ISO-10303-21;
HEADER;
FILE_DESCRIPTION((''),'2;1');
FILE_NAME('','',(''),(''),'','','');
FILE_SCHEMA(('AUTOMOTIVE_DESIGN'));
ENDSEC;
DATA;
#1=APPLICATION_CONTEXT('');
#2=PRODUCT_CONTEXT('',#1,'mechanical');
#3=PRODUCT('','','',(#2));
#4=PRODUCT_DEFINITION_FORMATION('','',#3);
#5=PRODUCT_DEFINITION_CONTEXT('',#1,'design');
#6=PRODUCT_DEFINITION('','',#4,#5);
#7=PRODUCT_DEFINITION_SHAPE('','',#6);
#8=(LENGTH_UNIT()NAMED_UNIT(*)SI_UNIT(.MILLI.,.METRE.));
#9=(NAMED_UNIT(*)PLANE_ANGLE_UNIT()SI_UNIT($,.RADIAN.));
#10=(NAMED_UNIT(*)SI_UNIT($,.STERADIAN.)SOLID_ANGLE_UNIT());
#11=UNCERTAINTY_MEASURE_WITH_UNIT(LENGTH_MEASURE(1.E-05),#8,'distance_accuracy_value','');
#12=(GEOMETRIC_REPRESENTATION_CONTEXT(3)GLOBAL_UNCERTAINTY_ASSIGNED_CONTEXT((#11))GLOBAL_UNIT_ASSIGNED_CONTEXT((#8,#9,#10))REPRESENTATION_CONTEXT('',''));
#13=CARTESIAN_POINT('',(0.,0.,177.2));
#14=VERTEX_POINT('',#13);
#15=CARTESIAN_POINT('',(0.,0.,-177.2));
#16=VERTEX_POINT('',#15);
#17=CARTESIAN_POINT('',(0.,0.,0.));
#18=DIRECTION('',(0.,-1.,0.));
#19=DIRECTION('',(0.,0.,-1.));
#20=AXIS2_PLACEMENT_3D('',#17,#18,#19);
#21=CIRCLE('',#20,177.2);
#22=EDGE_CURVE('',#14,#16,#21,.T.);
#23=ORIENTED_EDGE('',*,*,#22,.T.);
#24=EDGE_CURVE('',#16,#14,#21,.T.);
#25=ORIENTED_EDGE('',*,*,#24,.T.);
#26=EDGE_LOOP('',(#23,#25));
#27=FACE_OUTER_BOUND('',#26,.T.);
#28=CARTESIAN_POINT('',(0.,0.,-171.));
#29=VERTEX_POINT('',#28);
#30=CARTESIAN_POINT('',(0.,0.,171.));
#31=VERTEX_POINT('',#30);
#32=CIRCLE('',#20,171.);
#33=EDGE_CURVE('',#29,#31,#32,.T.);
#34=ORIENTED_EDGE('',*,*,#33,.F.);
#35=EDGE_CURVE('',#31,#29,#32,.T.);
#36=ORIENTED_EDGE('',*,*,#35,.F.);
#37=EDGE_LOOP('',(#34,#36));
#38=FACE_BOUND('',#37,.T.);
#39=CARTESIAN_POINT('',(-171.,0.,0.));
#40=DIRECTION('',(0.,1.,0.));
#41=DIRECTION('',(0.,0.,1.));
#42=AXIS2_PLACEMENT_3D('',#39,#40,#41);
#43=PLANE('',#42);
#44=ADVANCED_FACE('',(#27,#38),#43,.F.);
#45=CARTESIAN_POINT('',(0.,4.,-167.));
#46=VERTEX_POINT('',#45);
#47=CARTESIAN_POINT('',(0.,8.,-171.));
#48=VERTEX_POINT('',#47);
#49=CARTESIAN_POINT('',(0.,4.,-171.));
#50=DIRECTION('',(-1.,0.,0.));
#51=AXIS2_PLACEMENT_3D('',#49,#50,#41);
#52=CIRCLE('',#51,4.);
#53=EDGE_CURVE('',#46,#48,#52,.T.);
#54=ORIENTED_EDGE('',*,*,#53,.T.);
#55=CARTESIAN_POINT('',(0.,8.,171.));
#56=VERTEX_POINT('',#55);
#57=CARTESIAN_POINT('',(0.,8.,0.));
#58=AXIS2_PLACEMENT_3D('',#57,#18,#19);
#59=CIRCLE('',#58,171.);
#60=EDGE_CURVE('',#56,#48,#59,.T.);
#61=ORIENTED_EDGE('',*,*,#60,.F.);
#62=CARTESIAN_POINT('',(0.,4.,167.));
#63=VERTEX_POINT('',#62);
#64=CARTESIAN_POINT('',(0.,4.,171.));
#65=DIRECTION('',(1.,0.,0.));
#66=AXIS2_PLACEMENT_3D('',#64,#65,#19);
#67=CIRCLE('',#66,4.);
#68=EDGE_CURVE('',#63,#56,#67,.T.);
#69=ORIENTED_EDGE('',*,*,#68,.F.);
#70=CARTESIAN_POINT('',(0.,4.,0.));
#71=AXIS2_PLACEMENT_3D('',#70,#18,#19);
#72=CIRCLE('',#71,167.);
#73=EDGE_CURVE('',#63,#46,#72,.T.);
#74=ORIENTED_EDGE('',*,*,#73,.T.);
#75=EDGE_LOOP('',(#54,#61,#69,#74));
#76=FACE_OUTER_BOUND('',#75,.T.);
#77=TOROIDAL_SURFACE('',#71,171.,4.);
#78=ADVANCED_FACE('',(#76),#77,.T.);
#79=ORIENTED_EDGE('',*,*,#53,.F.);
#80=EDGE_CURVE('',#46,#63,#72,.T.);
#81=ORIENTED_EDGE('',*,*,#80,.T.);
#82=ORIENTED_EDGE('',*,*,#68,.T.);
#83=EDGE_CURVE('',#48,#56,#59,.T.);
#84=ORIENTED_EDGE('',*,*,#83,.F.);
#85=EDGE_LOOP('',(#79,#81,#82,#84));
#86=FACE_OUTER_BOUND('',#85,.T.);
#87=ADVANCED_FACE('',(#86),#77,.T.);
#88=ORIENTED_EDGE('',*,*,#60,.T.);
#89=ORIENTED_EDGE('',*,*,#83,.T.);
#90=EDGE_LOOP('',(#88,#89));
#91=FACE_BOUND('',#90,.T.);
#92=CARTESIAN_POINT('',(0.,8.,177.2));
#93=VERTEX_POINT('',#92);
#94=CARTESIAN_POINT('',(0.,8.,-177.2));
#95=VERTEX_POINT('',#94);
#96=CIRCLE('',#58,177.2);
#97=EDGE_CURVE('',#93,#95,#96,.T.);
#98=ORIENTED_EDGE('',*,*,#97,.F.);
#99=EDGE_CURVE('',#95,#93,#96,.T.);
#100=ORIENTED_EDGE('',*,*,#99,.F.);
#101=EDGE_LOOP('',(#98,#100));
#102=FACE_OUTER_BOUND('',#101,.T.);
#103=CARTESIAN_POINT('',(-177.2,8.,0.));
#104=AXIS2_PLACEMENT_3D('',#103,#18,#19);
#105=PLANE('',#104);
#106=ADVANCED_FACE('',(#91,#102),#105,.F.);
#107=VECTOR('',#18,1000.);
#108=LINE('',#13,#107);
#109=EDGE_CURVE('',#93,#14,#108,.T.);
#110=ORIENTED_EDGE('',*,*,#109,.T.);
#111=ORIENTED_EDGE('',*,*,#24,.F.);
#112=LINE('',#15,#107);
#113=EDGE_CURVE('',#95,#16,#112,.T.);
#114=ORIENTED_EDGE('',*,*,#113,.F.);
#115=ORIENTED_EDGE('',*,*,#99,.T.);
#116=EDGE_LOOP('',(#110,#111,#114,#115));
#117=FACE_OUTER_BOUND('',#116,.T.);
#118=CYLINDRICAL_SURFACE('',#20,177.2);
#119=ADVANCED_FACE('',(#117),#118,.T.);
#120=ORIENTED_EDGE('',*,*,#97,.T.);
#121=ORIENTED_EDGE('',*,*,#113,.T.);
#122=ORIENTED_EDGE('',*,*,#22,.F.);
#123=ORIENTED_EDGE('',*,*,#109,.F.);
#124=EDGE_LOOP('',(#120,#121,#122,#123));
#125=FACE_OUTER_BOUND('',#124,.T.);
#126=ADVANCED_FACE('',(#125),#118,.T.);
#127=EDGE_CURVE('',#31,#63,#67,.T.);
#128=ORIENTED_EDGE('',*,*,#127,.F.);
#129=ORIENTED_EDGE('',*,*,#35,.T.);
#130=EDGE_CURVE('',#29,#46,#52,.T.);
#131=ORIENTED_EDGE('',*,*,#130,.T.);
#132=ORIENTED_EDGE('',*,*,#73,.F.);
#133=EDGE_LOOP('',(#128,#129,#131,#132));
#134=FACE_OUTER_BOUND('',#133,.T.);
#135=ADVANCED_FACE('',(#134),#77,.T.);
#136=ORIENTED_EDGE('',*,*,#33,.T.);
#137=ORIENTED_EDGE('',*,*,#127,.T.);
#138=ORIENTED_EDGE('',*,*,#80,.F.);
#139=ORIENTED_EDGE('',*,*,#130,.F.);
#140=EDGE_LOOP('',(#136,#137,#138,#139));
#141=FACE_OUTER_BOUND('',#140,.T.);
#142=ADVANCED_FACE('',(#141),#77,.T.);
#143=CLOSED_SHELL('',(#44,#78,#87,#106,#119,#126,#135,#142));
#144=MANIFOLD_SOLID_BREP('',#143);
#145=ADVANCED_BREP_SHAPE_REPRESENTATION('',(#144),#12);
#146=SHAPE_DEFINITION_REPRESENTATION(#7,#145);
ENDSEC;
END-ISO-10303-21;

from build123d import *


with BuildPart() as part:
    # Sketch1 → Revolve1 (revolve)
    with BuildSketch(Plane.XY, mode=Mode.PRIVATE) as revolve1_sk:
        with BuildLine():
            Line((-171, 0), (-177.2, 0))
            Line((-177.2, 0), (-177.2, 8))
            Line((-177.2, 8), (-171, 8))
            ThreePointArc((-171, 8), (-167, 4), (-171, 0))
        make_face()
    revolve(revolve1_sk.sketch.rotate(Axis((0, 0, 0), (0, 1, 0)), 270), axis=Axis((0, 0, 0), (0, 1, 0)))


solid = part.part
